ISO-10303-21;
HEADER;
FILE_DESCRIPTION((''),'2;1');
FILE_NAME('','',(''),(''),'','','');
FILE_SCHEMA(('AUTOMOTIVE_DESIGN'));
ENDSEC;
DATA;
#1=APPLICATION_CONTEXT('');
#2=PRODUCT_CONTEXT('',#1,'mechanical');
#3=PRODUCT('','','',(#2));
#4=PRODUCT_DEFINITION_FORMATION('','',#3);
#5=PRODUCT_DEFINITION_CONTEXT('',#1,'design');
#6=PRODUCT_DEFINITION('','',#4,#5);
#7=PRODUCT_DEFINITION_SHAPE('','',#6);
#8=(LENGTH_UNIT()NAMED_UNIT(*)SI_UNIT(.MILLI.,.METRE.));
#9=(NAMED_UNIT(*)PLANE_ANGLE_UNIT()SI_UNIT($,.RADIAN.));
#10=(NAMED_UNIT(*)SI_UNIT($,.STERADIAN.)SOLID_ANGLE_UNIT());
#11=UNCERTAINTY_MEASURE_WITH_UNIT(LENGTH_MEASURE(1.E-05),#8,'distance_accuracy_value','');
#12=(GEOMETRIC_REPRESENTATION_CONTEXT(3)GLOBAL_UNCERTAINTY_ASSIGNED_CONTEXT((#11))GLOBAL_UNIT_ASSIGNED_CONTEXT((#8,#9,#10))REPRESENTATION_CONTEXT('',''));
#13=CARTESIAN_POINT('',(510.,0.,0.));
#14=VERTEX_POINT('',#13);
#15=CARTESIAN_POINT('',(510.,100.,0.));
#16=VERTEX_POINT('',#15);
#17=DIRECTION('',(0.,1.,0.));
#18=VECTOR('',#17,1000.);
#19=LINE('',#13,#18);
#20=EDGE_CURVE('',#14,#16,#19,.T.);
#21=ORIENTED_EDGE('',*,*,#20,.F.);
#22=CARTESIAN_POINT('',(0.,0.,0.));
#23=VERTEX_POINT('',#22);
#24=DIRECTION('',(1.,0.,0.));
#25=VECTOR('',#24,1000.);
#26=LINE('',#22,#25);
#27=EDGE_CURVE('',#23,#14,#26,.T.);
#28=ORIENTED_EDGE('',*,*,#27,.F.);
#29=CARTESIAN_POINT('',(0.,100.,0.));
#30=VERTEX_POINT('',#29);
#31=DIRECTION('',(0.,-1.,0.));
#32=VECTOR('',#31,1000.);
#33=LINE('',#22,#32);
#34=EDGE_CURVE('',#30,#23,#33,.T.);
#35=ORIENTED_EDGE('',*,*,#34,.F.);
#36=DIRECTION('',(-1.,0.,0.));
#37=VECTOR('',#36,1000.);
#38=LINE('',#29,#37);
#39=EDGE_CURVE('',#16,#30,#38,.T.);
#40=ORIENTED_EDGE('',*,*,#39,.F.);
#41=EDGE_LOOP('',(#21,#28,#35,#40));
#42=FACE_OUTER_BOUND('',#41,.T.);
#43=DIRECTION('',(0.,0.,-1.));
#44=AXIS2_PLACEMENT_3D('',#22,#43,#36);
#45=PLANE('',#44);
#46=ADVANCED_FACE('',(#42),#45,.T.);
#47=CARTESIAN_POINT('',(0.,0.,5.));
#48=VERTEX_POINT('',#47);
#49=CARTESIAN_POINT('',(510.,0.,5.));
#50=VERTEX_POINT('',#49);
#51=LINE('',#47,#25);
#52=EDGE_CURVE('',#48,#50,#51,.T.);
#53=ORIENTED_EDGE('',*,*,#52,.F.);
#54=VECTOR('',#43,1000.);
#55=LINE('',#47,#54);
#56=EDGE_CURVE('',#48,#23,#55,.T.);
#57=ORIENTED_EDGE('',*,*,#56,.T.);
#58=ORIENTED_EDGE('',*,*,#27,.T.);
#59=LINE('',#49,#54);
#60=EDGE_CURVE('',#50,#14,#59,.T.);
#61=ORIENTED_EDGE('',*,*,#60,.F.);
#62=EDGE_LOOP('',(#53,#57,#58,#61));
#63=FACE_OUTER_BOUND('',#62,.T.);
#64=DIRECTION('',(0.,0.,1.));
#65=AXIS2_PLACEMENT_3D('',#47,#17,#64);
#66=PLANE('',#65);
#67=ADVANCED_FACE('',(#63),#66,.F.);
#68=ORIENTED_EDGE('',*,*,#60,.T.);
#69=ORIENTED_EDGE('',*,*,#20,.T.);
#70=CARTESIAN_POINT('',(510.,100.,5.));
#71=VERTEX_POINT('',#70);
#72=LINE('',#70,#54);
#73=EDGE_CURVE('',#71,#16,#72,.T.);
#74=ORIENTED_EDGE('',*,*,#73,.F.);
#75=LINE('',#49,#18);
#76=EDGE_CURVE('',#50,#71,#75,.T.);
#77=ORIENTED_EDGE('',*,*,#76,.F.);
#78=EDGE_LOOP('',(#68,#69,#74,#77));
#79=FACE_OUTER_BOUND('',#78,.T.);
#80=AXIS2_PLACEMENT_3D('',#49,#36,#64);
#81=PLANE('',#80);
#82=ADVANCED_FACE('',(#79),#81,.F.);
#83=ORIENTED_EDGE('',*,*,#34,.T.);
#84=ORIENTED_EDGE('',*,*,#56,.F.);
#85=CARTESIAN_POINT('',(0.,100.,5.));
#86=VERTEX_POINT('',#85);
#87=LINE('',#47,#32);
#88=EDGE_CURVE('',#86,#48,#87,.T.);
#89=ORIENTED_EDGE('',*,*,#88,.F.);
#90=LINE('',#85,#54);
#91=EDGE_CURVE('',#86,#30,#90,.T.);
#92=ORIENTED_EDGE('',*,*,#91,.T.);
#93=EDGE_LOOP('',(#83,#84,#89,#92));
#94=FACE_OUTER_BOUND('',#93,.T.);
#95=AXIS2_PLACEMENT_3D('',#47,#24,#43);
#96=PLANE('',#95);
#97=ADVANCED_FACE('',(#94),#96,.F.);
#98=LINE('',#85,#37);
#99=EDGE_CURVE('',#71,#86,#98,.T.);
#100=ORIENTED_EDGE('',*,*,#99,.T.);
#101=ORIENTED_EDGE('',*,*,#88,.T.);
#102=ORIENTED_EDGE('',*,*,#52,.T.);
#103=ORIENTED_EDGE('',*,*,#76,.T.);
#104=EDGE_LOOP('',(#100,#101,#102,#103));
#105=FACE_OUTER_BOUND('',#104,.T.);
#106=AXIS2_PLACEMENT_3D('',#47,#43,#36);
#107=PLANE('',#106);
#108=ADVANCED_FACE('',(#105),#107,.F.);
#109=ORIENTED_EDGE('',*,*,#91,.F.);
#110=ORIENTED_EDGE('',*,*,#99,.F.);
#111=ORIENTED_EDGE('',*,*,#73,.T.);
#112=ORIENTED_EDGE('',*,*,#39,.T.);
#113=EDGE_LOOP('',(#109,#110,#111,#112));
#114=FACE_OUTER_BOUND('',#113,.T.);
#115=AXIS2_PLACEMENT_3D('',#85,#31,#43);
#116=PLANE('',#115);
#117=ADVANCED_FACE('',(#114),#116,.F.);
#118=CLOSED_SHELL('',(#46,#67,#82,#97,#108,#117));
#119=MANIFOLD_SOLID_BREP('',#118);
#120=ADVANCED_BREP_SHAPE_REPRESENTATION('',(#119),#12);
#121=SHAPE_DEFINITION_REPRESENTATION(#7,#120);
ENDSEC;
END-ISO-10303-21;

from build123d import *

# Parameters (mm, degrees)
SKETCH1_W           = 510
SKETCH1_H           = 100
BOSS_EXTRUDE1_DEPTH = 5


with BuildPart() as part:
    # Sketch1 → Boss-Extrude1 (new body)
    with BuildSketch(Plane.XY):
        with Locations((255, 50)):
            Rectangle(SKETCH1_W, SKETCH1_H)
    extrude(amount=BOSS_EXTRUDE1_DEPTH)


solid = part.part
